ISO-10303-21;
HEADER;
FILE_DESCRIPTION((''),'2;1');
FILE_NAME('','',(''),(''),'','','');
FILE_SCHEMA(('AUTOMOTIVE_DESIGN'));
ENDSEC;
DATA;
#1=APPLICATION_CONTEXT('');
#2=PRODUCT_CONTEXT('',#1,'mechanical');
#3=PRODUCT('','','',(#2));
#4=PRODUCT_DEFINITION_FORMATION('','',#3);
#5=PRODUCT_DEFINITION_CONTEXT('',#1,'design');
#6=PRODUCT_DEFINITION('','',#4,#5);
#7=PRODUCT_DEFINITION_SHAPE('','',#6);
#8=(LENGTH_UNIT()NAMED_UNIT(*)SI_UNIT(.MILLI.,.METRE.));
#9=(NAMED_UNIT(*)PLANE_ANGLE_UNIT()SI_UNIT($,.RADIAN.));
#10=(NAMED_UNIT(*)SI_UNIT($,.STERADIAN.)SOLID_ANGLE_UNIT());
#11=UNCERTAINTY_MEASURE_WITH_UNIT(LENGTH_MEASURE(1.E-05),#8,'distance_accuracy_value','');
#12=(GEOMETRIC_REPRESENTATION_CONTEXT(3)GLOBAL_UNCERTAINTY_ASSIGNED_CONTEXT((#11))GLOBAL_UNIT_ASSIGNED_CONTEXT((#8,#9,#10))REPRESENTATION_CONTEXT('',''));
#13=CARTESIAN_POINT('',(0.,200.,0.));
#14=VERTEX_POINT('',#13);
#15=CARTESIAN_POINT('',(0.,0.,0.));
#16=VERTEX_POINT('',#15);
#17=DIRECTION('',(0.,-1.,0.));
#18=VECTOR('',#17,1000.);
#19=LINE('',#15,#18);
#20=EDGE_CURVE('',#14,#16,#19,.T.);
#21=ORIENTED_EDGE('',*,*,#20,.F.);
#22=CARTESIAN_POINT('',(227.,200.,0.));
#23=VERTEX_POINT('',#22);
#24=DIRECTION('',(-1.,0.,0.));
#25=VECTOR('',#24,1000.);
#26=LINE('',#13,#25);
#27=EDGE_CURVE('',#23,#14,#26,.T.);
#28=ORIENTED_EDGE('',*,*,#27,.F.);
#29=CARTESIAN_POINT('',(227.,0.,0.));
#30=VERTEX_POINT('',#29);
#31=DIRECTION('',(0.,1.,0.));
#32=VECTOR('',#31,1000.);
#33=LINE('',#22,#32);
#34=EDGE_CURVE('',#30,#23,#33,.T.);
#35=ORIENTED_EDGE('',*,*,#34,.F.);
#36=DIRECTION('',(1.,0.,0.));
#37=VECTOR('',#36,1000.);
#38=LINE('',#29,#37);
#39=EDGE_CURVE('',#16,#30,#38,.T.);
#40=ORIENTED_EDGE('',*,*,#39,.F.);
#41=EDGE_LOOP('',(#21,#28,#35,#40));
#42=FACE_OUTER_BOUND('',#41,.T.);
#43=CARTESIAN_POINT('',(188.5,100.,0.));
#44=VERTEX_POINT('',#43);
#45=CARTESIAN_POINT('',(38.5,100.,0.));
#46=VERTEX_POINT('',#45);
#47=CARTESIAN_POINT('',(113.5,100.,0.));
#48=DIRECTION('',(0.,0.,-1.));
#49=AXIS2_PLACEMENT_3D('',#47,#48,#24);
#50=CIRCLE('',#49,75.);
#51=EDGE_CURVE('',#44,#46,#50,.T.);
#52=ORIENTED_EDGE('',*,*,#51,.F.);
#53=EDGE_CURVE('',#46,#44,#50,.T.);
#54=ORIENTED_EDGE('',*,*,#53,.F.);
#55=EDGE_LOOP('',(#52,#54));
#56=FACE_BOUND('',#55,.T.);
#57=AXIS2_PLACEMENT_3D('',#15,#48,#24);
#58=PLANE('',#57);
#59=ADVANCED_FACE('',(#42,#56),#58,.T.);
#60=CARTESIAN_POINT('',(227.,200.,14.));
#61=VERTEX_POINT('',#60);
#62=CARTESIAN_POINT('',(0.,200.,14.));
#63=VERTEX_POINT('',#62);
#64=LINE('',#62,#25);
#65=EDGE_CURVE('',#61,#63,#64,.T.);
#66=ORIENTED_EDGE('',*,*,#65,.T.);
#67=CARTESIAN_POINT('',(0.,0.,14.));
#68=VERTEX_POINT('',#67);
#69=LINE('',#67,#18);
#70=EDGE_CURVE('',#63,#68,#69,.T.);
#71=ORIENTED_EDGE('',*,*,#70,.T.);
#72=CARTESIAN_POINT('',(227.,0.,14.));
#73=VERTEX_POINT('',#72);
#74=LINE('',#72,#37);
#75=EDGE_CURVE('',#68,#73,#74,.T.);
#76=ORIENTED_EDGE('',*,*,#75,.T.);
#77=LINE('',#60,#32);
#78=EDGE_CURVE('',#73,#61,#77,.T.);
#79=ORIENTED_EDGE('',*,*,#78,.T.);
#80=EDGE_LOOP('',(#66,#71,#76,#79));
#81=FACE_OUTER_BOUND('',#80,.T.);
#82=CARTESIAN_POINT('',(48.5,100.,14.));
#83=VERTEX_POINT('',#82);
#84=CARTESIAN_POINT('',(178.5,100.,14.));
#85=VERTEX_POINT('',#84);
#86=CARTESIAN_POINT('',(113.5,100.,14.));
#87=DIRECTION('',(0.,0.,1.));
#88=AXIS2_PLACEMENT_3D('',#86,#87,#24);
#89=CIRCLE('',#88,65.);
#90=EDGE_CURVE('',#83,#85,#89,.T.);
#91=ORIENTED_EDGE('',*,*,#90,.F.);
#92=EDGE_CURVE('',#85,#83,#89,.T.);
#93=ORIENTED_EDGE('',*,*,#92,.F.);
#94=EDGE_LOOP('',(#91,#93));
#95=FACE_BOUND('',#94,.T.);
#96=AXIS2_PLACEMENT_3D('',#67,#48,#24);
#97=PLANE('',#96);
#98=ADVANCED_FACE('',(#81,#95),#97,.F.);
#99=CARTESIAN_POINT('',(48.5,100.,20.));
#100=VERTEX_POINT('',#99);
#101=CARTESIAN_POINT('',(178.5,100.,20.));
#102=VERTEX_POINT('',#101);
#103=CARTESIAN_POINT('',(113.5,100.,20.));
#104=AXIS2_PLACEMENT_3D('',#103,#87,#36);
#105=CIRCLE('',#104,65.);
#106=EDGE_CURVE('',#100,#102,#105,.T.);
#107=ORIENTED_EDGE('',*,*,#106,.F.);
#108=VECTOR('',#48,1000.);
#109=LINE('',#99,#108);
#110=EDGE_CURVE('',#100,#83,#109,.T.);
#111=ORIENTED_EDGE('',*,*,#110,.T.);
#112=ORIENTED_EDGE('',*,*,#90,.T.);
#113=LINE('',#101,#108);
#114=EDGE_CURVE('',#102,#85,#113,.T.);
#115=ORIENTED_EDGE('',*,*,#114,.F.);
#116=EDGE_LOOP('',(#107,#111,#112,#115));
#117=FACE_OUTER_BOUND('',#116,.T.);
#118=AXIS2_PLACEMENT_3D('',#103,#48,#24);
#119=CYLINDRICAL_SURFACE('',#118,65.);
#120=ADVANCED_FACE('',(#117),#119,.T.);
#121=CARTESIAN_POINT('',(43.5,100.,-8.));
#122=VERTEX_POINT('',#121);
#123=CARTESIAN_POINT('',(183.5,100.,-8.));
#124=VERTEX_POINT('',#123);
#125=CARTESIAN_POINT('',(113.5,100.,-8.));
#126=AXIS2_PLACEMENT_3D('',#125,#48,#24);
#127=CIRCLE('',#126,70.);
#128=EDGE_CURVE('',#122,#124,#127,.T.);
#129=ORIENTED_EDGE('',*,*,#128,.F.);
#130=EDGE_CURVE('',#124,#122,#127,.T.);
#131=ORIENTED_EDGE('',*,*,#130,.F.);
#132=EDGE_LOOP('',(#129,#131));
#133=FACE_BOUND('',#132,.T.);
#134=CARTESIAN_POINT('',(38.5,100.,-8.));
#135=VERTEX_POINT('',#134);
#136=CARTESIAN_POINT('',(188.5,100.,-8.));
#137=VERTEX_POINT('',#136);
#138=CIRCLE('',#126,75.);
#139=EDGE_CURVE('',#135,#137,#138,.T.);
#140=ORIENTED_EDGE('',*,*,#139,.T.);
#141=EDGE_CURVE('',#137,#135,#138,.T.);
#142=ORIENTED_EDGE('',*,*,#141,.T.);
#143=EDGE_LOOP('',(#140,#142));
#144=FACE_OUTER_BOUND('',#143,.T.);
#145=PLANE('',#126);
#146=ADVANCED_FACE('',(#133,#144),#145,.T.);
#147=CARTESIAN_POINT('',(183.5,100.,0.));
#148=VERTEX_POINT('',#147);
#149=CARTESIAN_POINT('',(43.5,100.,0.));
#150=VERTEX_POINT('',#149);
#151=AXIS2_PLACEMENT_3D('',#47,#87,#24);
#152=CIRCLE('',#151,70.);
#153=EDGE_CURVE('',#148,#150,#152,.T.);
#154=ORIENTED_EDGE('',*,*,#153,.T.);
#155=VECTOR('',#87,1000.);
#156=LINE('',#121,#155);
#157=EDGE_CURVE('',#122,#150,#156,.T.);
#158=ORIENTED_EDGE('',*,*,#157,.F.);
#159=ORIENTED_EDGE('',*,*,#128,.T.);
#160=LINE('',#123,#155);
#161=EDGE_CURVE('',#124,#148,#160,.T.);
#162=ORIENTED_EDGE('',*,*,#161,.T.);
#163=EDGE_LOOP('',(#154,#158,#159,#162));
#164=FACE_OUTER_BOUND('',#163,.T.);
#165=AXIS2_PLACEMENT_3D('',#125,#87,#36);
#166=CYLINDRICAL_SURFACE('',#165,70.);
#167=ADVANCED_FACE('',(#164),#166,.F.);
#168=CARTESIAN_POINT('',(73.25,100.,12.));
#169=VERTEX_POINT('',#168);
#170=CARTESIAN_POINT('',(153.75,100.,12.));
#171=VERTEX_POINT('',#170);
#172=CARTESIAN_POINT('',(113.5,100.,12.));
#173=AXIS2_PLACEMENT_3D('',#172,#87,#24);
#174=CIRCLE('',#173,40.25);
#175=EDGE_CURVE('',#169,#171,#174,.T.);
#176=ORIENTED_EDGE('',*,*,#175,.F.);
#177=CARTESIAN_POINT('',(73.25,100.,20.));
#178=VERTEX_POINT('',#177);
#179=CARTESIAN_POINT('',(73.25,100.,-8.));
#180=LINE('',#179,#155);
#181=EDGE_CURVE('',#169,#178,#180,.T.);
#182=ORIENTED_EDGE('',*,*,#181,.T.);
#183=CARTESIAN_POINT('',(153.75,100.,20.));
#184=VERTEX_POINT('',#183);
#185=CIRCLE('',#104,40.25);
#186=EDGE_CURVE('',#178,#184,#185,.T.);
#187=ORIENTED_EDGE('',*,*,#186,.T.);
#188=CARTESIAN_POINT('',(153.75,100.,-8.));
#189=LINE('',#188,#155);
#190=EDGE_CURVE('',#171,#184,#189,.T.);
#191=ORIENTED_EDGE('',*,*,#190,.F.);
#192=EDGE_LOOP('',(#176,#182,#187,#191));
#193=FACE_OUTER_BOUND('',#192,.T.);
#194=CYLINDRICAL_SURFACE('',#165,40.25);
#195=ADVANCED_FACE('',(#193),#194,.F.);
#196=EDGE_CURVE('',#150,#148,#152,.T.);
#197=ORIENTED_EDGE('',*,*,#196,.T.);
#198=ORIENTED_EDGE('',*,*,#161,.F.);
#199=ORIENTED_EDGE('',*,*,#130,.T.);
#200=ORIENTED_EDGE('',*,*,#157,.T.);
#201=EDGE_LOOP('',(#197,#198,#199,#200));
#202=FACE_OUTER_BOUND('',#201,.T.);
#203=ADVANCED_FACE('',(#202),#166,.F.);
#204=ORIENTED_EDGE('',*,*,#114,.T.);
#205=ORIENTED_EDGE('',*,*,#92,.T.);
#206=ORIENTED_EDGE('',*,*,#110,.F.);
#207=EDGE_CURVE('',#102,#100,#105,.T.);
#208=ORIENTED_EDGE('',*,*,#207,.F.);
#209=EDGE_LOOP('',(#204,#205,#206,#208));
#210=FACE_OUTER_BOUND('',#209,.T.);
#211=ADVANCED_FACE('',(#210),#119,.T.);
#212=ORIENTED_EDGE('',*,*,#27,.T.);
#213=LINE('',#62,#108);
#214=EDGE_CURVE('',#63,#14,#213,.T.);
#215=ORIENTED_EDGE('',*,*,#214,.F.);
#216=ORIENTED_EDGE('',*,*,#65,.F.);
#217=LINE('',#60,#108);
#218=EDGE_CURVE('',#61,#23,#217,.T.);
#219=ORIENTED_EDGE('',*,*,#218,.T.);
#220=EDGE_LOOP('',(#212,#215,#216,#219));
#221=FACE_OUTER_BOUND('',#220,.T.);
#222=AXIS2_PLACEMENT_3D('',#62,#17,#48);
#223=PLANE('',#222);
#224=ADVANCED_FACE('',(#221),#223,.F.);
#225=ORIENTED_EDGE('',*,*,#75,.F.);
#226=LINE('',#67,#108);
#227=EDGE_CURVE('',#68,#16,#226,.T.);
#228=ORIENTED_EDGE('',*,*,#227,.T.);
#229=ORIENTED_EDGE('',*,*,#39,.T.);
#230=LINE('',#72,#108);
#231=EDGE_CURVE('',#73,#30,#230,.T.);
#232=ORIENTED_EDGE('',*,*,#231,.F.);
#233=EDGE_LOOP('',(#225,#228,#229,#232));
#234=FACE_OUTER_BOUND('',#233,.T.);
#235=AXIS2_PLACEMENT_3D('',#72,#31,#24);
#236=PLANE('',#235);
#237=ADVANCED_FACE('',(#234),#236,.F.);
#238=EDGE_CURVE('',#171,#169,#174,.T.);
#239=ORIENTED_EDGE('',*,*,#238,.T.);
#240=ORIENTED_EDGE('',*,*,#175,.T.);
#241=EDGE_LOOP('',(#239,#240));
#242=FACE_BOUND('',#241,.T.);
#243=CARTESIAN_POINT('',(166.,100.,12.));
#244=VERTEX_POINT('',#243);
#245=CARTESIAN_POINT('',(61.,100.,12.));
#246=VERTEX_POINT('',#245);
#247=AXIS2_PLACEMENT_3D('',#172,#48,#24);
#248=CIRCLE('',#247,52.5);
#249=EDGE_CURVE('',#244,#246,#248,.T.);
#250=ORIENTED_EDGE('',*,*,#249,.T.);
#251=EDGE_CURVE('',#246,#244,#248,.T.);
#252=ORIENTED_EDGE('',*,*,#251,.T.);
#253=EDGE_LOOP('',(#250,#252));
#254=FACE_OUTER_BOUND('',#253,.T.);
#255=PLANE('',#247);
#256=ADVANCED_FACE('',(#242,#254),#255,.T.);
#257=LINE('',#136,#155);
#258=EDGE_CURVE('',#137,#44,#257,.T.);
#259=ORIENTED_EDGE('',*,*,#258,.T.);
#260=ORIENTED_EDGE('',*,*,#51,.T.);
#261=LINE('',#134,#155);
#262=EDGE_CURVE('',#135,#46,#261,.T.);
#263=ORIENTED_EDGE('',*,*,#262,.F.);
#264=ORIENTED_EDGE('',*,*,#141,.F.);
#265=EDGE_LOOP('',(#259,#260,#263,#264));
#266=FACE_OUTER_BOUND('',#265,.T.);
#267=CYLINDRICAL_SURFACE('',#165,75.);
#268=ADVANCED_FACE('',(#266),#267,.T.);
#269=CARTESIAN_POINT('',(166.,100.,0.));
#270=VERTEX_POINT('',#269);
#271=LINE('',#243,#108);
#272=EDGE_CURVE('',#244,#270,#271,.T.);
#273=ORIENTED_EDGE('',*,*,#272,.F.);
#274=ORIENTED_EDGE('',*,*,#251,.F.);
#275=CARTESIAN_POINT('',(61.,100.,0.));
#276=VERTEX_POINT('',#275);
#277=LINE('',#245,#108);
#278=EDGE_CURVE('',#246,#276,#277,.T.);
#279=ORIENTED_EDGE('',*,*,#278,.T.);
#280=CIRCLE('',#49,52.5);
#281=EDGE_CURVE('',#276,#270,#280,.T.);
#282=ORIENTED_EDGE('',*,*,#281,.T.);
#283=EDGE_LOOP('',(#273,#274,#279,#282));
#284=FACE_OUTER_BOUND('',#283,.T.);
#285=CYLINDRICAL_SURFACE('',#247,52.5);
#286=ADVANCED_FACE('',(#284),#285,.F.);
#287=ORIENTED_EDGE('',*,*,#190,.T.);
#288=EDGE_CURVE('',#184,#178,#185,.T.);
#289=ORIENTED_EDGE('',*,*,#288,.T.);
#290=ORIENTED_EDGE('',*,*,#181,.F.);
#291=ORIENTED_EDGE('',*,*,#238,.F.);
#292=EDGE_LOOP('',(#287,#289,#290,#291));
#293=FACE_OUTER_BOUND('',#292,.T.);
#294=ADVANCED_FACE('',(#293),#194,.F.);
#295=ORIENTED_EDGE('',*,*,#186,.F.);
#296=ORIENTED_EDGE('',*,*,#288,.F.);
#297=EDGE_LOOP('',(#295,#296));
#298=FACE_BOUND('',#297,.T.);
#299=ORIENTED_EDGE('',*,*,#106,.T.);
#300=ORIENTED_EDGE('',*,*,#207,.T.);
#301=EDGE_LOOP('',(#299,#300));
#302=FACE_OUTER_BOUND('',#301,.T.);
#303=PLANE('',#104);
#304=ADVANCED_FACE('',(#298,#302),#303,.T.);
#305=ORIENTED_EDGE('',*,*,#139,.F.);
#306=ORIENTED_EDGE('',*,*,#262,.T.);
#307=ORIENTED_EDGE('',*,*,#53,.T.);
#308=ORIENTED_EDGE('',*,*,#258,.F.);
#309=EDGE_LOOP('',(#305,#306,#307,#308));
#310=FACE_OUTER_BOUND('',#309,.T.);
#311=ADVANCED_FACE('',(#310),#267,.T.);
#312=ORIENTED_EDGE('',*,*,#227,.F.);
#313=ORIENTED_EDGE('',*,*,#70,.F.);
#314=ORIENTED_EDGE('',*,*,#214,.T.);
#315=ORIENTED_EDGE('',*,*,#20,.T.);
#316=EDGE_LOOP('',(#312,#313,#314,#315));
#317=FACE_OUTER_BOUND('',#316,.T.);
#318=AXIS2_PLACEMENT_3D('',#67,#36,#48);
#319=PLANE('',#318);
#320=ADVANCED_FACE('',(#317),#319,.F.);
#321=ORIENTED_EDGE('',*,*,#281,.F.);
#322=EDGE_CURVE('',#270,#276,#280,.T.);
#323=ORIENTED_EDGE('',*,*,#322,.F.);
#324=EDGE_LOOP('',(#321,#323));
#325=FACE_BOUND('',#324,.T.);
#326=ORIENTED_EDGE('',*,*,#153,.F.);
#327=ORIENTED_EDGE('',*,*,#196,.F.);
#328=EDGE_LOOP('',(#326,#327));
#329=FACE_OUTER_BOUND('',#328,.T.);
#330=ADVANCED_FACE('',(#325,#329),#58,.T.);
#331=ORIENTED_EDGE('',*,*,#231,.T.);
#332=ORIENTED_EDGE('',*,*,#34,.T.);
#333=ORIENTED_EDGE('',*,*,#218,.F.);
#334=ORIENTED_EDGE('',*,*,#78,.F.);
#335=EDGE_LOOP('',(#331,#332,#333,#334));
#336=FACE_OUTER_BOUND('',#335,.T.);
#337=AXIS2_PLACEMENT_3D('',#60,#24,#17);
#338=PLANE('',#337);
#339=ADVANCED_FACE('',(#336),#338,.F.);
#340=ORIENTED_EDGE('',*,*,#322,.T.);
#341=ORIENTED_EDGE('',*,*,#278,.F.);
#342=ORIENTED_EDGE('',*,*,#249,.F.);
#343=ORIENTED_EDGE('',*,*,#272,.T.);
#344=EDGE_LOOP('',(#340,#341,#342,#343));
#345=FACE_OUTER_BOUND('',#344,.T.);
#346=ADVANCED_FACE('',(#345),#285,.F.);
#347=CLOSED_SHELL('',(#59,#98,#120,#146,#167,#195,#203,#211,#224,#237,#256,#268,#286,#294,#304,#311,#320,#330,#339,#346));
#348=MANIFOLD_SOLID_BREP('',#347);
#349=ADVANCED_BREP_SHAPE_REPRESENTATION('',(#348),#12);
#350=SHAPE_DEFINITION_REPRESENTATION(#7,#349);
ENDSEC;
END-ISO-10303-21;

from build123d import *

# Parameters (mm, degrees)
SKETCH1_W           = 227
SKETCH1_H           = 200
BOSS_EXTRUDE1_DEPTH = 14
SKETCH2_R           = 65
BOSS_EXTRUDE2_DEPTH = 6
SKETCH3_R           = 75
SKETCH3_R_2         = 70
BOSS_EXTRUDE3_DEPTH = 8
SKETCH4_R           = 40.25
CUT_EXTRUDE1_DEPTH  = 304.830544877
SKETCH5_R           = 52.5
CUT_EXTRUDE2_DEPTH  = 12


with BuildPart() as part:
    # Sketch1 → Boss-Extrude1 (new body)
    with BuildSketch(Plane.XY):
        with Locations((113.5, 100)):
            Rectangle(SKETCH1_W, SKETCH1_H)
    extrude(amount=BOSS_EXTRUDE1_DEPTH)

    # Sketch2 → Boss-Extrude2 (add)
    with BuildSketch(Plane.XY.offset(14)):
        with Locations(Location((113.5, 100, 0), (0, 0, 180))):
            Circle(SKETCH2_R)
    extrude(amount=BOSS_EXTRUDE2_DEPTH)

    # Sketch3 → Boss-Extrude3 (add)
    with BuildSketch(Plane(origin=(0, 0, 0), x_dir=(-1, 0, 0), z_dir=(0, 0, -1))):
        with Locations((-113.5, 100)):
            Circle(SKETCH3_R)
        with Locations((-113.5, 100)):
            Circle(SKETCH3_R_2, mode=Mode.SUBTRACT)
    extrude(amount=BOSS_EXTRUDE3_DEPTH)

    # Sketch4 → Cut-Extrude1 (cut, through all)
    with BuildSketch(Plane.XY.offset(20)):
        with Locations((113.5, 100)):
            Circle(SKETCH4_R)
    extrude(amount=-CUT_EXTRUDE1_DEPTH, mode=Mode.SUBTRACT)

    # Sketch5 → Cut-Extrude2 (cut)
    with BuildSketch(Plane(origin=(0, 0, 0), x_dir=(-1, 0, 0), z_dir=(0, 0, -1))):
        with Locations((-113.5, 100)):
            Circle(SKETCH5_R)
    extrude(amount=-CUT_EXTRUDE2_DEPTH, mode=Mode.SUBTRACT)


solid = part.part
